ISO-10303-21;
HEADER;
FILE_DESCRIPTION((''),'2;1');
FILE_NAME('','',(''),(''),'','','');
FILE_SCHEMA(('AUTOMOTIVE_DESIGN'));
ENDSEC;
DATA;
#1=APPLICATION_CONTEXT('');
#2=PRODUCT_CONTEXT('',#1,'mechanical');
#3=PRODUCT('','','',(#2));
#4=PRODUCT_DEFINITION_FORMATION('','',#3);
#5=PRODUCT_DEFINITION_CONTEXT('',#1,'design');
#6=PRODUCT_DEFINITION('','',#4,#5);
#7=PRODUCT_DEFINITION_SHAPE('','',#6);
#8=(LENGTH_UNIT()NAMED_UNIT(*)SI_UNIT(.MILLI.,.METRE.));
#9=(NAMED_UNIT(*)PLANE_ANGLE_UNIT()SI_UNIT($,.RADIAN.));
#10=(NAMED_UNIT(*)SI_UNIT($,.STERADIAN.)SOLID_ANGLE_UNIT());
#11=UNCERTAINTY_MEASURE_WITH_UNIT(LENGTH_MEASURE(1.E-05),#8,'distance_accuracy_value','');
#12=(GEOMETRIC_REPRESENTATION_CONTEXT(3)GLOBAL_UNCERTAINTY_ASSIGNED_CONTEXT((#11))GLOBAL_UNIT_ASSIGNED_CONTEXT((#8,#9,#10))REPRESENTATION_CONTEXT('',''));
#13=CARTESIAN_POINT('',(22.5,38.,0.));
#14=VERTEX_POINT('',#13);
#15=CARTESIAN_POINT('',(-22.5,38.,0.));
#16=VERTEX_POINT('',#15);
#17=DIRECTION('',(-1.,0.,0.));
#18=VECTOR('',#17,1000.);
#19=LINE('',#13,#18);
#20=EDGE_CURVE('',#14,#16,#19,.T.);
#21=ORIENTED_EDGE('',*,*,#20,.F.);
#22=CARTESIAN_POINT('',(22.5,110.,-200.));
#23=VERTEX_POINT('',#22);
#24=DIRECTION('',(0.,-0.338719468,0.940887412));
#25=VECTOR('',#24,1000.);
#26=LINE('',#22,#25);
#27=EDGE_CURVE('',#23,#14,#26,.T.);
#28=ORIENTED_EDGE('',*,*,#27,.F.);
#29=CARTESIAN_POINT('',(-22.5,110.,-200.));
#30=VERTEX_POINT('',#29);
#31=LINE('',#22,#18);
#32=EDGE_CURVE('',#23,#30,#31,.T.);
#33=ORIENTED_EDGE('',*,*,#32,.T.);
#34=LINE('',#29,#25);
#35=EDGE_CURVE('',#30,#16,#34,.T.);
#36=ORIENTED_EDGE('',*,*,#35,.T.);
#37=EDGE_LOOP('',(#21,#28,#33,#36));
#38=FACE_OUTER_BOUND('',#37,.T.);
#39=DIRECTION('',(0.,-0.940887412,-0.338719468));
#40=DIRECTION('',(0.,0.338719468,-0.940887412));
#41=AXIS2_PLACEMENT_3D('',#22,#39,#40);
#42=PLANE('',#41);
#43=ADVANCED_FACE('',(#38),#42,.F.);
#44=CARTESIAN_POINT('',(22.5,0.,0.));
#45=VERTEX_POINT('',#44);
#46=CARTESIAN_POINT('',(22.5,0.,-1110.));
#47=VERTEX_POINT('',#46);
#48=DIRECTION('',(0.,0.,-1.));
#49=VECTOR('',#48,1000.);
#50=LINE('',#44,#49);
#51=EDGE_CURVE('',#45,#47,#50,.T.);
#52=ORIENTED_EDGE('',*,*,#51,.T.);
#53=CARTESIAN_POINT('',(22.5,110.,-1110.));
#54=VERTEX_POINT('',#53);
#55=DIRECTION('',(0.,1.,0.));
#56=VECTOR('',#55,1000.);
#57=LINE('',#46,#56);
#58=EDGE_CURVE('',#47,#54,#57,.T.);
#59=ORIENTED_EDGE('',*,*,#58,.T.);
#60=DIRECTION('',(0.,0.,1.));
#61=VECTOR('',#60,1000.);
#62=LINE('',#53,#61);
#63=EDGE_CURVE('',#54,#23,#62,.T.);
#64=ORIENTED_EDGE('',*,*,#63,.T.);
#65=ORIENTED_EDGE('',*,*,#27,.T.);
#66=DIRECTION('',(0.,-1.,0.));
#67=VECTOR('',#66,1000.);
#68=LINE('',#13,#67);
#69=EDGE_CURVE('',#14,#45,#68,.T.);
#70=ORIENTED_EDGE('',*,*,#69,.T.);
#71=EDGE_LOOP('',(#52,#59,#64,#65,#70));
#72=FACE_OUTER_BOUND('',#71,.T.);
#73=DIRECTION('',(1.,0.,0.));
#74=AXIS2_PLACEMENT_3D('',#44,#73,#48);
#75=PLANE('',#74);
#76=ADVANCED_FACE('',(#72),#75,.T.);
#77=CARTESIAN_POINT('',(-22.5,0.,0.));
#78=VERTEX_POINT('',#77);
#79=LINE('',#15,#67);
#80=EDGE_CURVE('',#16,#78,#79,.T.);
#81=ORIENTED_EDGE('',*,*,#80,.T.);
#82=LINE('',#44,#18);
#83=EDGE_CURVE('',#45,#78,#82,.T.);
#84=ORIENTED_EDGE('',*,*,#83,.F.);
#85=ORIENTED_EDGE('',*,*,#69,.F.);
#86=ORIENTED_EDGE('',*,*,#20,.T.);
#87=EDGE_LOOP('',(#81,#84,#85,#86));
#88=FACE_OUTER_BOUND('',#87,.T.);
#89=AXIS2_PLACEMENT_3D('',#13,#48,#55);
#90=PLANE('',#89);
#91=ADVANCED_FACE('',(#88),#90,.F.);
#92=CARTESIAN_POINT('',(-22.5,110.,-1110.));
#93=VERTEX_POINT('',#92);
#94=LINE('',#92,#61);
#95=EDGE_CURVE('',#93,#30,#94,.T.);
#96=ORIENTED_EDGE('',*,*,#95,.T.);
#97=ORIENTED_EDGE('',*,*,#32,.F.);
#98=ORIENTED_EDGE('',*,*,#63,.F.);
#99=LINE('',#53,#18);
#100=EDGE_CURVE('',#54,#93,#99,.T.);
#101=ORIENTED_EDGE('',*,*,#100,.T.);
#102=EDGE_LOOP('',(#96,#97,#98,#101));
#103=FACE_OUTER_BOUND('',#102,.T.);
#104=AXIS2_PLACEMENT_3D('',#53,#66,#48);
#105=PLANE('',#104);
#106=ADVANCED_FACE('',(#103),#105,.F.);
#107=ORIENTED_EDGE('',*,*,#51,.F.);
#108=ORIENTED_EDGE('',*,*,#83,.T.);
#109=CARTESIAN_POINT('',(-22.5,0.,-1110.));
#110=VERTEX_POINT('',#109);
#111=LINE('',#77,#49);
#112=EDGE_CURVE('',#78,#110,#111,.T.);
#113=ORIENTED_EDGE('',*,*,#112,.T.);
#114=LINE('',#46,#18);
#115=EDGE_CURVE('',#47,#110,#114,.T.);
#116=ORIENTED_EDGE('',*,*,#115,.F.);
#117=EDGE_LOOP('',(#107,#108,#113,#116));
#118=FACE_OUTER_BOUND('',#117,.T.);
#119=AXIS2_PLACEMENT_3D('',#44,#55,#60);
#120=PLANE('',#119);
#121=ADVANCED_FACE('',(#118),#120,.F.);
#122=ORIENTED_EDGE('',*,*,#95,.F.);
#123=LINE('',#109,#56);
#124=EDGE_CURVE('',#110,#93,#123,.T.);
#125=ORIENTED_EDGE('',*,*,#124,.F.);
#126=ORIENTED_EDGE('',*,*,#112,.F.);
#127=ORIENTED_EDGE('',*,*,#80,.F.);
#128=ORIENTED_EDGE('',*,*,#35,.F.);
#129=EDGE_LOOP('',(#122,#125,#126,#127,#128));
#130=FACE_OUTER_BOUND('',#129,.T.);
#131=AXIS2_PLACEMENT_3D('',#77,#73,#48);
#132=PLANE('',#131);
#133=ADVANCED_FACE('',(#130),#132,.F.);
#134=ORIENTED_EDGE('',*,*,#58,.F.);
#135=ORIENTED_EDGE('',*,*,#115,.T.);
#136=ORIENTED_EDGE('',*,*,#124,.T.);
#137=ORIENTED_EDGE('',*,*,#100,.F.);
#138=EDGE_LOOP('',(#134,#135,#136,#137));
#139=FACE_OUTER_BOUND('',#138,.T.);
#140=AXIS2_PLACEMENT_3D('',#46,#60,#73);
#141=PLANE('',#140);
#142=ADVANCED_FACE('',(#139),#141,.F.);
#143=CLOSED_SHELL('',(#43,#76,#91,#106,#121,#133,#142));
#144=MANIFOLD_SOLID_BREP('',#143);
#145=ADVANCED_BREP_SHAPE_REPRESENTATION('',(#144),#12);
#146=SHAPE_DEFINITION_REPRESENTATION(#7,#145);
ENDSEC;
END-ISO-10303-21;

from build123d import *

# Parameters (mm, degrees)
BOSS_EXTRUDE1_DEPTH = 22.5


with BuildPart() as part:
    # Sketch1 → Boss-Extrude1 (new, symmetric)
    with BuildSketch(Plane(origin=(0, 0, 0), x_dir=(0, 0, -1), z_dir=(1, 0, 0))):
        Polygon((0, 0), (1110, 0), (1110, 110), (200, 110), (0, 38), align=None)
    extrude(amount=BOSS_EXTRUDE1_DEPTH, both=True)


solid = part.part
